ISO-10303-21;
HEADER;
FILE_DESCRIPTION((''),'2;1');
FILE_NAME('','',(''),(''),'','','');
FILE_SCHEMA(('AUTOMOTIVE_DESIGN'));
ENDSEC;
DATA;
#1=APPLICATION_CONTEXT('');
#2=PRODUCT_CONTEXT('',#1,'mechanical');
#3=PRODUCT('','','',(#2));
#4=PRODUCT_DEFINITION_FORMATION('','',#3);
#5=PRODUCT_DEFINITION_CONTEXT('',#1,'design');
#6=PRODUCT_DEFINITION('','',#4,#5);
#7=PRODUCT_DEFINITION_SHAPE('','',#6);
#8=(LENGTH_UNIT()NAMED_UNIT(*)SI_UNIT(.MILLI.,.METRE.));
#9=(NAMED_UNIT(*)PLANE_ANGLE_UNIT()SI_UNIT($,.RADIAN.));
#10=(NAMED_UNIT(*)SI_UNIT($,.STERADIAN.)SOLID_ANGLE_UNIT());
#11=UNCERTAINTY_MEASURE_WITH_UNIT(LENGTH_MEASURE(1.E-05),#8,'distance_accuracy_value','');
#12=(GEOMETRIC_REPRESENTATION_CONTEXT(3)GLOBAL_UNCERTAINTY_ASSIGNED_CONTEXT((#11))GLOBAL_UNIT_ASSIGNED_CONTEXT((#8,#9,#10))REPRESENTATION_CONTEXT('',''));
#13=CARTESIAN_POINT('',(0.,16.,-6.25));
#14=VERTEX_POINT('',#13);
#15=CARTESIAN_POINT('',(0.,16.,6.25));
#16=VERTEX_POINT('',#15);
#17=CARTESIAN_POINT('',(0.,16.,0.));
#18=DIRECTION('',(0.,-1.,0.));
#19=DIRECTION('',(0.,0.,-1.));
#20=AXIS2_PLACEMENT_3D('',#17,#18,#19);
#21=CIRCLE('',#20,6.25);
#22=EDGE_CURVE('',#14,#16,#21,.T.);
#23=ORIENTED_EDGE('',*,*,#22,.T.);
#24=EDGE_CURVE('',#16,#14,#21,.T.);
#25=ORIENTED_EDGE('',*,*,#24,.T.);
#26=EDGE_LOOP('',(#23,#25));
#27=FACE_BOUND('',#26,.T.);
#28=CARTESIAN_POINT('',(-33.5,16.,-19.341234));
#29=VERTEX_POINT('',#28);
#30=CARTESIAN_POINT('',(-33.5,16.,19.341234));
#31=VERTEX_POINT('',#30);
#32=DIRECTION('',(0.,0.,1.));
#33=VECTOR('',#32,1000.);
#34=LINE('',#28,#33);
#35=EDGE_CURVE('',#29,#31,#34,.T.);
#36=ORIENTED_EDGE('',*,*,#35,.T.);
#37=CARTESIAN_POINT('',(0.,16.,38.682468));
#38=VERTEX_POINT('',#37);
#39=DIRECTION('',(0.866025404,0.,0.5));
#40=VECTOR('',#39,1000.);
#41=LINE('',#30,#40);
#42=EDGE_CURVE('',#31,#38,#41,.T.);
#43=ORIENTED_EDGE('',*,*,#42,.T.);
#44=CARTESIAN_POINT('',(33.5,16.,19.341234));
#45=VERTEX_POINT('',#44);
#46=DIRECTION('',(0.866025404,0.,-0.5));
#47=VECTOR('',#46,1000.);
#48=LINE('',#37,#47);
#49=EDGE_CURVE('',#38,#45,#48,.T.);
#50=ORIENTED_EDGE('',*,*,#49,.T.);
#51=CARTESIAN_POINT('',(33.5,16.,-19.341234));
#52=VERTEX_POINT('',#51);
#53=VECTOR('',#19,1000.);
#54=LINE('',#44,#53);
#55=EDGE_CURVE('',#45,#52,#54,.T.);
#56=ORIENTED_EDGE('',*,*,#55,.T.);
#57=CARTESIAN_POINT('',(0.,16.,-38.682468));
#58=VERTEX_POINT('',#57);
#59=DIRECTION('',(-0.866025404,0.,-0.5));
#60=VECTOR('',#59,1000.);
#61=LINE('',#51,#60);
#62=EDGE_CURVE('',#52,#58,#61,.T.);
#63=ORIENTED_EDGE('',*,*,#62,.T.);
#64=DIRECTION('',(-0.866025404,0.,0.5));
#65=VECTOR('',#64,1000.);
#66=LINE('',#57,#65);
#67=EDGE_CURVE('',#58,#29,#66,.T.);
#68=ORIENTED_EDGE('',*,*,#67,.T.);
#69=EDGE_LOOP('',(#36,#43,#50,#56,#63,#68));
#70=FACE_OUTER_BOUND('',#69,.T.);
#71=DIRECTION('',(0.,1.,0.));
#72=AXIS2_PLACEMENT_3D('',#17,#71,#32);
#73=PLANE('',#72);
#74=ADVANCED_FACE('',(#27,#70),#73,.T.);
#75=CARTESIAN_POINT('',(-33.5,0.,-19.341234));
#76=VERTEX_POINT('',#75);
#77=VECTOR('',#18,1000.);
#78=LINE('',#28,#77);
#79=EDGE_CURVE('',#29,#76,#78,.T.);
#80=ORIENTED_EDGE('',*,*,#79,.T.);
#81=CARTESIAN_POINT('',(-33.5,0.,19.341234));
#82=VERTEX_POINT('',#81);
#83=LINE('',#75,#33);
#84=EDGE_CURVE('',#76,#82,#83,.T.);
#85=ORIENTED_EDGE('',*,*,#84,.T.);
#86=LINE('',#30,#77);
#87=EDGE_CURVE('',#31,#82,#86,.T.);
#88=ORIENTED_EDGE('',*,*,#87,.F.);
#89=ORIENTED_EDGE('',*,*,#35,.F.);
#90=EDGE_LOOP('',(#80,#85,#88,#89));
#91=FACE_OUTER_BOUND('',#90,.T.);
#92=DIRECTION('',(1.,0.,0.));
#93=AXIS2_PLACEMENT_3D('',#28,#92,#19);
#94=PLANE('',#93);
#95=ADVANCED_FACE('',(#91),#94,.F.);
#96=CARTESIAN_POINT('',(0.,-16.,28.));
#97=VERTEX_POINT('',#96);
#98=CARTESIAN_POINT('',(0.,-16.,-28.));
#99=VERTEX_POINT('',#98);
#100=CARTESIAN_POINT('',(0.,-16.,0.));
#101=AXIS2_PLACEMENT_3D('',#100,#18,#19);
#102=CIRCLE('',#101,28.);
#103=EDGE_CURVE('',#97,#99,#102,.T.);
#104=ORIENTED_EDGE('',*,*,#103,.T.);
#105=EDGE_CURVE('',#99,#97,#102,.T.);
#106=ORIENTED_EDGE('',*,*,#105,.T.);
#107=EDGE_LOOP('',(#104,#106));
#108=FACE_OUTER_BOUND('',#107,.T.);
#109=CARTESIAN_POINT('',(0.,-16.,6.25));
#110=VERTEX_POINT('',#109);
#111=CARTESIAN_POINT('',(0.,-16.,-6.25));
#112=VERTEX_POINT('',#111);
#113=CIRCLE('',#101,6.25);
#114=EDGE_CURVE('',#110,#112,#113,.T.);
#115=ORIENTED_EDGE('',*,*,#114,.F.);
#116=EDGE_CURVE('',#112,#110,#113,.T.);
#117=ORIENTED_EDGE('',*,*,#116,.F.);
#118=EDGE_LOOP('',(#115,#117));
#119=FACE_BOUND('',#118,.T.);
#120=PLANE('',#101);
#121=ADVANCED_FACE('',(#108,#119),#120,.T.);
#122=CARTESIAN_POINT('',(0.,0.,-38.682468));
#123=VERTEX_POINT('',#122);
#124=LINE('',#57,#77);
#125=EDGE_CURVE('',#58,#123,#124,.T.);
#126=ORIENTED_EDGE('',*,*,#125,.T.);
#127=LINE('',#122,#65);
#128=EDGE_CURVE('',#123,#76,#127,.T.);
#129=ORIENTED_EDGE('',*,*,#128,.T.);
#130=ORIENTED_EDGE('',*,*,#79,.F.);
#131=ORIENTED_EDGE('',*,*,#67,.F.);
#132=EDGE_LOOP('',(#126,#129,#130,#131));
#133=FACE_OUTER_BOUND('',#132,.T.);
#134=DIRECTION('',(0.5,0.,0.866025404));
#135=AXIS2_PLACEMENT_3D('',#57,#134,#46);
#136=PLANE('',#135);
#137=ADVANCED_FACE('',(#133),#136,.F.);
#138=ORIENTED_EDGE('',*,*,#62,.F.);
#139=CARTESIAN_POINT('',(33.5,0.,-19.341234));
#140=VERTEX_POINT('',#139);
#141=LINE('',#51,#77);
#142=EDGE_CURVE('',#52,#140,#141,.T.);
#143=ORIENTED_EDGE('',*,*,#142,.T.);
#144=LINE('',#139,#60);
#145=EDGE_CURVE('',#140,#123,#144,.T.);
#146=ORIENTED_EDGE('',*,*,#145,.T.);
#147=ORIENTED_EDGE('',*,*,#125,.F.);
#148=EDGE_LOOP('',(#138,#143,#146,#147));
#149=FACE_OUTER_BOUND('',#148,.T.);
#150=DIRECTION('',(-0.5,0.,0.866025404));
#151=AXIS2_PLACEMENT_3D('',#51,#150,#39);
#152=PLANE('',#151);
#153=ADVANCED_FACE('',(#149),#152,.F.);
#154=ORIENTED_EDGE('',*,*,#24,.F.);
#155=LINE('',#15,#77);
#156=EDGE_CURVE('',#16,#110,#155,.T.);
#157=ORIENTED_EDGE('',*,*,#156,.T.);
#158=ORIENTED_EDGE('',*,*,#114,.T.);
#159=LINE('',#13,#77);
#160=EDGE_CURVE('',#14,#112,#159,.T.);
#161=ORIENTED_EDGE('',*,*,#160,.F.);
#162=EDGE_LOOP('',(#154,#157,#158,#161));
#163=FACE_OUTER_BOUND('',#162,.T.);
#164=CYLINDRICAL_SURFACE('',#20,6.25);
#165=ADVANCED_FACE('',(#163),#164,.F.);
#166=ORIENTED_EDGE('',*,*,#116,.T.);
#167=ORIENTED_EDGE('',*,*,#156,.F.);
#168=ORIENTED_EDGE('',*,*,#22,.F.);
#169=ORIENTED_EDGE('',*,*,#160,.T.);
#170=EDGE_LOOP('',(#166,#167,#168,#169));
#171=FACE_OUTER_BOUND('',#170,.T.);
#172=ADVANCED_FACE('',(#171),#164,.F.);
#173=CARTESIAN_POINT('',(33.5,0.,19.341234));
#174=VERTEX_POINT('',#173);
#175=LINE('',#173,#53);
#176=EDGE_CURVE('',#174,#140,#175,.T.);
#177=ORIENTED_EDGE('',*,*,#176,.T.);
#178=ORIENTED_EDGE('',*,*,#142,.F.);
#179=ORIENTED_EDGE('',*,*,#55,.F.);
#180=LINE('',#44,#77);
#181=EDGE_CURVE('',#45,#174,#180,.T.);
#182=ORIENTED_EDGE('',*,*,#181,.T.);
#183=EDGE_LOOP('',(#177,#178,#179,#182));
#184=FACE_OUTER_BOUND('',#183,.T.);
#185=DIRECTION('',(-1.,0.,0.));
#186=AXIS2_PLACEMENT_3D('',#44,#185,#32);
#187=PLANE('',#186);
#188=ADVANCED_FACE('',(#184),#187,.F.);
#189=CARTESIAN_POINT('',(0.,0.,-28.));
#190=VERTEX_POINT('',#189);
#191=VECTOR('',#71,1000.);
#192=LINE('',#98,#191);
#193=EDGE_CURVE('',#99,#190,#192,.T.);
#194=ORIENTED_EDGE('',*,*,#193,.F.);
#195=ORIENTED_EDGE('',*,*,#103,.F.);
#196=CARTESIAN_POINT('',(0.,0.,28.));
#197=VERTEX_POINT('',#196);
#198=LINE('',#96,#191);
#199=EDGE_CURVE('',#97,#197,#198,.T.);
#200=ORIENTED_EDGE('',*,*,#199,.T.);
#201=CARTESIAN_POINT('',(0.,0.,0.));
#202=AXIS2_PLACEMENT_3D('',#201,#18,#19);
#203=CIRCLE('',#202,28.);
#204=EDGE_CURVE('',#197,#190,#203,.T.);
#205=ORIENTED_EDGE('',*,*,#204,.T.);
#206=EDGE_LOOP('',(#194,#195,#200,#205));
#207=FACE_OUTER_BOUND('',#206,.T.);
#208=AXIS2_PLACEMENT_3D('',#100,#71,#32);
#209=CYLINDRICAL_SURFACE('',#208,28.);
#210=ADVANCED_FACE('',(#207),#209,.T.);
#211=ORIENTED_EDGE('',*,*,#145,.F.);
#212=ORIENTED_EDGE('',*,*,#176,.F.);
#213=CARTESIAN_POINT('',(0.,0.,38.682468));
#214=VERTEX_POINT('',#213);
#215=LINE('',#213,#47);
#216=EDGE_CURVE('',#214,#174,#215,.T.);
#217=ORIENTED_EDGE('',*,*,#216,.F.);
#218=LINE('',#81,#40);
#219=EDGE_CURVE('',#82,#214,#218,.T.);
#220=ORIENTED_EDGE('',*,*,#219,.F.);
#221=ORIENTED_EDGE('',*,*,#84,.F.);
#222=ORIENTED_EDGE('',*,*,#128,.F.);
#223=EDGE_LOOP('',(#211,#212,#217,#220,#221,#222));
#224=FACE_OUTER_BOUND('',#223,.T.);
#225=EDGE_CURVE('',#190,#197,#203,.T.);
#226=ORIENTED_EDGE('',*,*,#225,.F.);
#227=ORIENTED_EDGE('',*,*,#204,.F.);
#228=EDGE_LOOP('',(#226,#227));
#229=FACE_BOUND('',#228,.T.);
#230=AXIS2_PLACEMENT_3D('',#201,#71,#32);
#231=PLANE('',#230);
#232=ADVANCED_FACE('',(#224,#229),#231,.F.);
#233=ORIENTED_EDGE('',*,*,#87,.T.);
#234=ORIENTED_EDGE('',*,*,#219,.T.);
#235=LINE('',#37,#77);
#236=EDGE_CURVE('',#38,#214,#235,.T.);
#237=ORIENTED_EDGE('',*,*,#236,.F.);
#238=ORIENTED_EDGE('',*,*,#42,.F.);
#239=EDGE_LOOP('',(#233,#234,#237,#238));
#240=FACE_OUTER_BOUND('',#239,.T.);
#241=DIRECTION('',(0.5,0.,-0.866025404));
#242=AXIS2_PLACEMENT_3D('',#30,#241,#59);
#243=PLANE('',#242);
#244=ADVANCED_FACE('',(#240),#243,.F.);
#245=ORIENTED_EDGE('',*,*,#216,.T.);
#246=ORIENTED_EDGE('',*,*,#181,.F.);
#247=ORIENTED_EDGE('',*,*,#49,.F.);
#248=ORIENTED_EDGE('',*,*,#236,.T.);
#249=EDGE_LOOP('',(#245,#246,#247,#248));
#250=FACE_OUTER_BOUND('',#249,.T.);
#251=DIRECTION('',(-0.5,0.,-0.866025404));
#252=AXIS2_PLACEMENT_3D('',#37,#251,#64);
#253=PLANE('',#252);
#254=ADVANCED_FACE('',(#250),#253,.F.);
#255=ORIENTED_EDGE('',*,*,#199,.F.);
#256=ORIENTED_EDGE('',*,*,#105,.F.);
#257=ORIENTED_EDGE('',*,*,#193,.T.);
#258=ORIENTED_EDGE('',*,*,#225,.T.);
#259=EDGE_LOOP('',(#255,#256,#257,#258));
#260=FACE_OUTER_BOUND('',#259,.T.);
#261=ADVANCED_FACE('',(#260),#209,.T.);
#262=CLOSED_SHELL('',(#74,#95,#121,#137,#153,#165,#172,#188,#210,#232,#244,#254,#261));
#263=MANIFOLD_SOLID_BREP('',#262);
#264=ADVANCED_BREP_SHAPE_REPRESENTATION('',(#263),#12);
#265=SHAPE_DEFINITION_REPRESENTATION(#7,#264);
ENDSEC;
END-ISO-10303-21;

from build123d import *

# Parameters (mm, degrees)
HEX_BODY_67AF_X16_DEPTH = 16
COLLAR_PROFILE_56_R     = 28
COLLAR_56_X16_DEPTH     = 16
BORE_PROFILE_12_5_R     = 6.25
BORE_12_5_THROUGH_DEPTH = 61.353817885


with BuildPart() as part:
    # Hex Profile 67AF → Hex Body 67AF x16 (new body)
    with BuildSketch(Plane(origin=(0, 0, 0), x_dir=(1, 0, 0), z_dir=(0, 1, 0))):
        Polygon((0, -38.682468036), (33.5, -19.341234018), (33.5, 19.341234018), (0, 38.682468036), (-33.5, 19.341234018), (-33.5, -19.341234018), align=None)
    extrude(amount=HEX_BODY_67AF_X16_DEPTH)

    # Collar Profile Ø56 → Collar Ø56 x16 (add)
    with BuildSketch(Plane.XZ):
        with Locations(Location((0, 0, 0), (0, 0, 270))):
            Circle(COLLAR_PROFILE_56_R)
    extrude(amount=COLLAR_56_X16_DEPTH)

    # Bore Profile Ø12.5 → Bore Ø12.5 Through (cut, through all)
    with BuildSketch(Plane.XZ.offset(16)):
        with Locations(Location((0, 0, 0), (0, 0, 270))):
            Circle(BORE_PROFILE_12_5_R)
    extrude(amount=-BORE_12_5_THROUGH_DEPTH, mode=Mode.SUBTRACT)


solid = part.part
